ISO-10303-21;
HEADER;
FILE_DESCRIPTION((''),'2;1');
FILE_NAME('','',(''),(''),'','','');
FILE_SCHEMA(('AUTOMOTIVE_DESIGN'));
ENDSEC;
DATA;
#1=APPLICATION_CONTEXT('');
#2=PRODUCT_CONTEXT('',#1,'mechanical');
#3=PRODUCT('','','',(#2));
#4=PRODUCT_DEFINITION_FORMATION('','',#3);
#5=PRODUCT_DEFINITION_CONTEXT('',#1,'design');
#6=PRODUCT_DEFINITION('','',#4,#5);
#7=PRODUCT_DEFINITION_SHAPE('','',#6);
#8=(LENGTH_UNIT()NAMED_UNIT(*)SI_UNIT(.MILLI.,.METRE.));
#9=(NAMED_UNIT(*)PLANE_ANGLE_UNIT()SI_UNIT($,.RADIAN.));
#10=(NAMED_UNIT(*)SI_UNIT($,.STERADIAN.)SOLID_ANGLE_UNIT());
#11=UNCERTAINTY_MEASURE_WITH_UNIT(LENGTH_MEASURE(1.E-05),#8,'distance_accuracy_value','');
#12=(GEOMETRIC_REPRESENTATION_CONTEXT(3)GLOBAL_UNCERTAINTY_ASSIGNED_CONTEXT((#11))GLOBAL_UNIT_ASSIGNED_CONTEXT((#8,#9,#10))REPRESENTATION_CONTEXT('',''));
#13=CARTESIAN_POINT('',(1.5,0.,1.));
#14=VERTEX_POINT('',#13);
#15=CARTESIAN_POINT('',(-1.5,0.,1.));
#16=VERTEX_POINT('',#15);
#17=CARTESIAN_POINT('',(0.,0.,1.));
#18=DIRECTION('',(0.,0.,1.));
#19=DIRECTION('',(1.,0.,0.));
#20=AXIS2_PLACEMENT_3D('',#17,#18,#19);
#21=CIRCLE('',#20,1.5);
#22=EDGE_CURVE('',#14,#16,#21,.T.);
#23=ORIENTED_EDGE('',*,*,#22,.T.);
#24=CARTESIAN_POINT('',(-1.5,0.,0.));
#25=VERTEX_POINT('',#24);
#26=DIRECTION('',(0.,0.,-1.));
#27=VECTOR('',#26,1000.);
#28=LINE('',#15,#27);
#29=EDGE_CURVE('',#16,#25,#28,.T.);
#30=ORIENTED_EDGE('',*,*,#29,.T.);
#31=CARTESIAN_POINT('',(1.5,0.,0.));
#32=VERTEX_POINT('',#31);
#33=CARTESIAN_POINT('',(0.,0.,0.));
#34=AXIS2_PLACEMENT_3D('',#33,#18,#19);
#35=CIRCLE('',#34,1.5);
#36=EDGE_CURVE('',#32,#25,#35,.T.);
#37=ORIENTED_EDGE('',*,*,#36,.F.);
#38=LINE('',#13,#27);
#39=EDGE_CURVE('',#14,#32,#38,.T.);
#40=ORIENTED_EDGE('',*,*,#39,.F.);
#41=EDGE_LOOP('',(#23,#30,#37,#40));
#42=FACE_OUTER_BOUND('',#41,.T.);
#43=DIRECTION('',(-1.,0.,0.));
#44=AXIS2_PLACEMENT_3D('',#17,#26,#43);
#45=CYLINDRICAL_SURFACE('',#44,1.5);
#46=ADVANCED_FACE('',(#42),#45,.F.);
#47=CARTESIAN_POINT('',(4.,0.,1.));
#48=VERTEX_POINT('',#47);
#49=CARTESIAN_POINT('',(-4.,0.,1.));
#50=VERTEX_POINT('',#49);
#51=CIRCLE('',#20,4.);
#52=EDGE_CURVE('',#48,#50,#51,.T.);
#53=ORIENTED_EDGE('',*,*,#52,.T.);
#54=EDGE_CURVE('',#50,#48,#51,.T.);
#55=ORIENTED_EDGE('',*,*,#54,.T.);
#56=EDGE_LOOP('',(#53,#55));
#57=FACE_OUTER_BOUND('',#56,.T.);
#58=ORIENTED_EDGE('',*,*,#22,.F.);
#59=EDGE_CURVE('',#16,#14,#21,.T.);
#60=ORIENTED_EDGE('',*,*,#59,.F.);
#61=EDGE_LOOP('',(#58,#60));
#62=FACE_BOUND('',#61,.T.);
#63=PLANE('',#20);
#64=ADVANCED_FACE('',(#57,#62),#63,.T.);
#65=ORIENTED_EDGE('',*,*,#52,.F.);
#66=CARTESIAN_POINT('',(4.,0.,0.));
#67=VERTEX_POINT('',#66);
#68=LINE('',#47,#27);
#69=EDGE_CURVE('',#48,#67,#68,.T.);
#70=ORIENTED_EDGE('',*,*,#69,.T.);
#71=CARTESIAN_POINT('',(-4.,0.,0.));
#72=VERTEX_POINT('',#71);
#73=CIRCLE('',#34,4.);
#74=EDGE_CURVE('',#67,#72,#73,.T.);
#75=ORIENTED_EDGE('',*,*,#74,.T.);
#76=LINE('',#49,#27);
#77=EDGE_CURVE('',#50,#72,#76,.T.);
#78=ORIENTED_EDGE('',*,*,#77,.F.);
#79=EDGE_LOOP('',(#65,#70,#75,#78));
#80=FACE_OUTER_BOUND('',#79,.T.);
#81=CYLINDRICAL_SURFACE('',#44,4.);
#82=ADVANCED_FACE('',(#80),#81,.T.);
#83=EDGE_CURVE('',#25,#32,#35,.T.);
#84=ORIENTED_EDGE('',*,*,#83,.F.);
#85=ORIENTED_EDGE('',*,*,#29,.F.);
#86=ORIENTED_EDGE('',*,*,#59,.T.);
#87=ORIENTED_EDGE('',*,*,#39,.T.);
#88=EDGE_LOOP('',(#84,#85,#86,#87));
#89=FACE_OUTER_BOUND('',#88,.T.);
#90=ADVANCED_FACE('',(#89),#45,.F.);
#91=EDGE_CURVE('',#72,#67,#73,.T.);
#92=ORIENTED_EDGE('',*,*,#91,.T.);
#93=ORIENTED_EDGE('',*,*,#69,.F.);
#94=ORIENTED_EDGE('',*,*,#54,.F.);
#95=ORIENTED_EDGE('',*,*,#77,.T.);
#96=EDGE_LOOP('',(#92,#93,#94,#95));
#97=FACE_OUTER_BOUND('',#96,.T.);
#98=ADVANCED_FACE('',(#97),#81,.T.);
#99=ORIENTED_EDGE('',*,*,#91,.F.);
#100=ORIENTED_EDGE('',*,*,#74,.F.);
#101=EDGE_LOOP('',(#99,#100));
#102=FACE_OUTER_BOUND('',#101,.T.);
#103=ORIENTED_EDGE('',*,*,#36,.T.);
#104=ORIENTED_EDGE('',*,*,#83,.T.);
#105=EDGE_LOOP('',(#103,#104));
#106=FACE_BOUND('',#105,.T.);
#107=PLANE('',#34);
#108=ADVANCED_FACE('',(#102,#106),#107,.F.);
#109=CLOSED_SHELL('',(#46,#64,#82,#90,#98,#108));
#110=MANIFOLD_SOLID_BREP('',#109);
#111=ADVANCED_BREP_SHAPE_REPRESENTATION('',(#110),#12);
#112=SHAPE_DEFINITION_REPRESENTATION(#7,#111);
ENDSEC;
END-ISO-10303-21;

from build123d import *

# Parameters (mm, degrees)
SKETCH1_R           = 4
SKETCH1_R_2         = 1.5
BOSS_EXTRUDE1_DEPTH = 1


with BuildPart() as part:
    # Sketch1 → Boss-Extrude1 (new body)
    with BuildSketch(Plane.XY):
        Circle(SKETCH1_R)
        Circle(SKETCH1_R_2, mode=Mode.SUBTRACT)
    extrude(amount=BOSS_EXTRUDE1_DEPTH)


solid = part.part
